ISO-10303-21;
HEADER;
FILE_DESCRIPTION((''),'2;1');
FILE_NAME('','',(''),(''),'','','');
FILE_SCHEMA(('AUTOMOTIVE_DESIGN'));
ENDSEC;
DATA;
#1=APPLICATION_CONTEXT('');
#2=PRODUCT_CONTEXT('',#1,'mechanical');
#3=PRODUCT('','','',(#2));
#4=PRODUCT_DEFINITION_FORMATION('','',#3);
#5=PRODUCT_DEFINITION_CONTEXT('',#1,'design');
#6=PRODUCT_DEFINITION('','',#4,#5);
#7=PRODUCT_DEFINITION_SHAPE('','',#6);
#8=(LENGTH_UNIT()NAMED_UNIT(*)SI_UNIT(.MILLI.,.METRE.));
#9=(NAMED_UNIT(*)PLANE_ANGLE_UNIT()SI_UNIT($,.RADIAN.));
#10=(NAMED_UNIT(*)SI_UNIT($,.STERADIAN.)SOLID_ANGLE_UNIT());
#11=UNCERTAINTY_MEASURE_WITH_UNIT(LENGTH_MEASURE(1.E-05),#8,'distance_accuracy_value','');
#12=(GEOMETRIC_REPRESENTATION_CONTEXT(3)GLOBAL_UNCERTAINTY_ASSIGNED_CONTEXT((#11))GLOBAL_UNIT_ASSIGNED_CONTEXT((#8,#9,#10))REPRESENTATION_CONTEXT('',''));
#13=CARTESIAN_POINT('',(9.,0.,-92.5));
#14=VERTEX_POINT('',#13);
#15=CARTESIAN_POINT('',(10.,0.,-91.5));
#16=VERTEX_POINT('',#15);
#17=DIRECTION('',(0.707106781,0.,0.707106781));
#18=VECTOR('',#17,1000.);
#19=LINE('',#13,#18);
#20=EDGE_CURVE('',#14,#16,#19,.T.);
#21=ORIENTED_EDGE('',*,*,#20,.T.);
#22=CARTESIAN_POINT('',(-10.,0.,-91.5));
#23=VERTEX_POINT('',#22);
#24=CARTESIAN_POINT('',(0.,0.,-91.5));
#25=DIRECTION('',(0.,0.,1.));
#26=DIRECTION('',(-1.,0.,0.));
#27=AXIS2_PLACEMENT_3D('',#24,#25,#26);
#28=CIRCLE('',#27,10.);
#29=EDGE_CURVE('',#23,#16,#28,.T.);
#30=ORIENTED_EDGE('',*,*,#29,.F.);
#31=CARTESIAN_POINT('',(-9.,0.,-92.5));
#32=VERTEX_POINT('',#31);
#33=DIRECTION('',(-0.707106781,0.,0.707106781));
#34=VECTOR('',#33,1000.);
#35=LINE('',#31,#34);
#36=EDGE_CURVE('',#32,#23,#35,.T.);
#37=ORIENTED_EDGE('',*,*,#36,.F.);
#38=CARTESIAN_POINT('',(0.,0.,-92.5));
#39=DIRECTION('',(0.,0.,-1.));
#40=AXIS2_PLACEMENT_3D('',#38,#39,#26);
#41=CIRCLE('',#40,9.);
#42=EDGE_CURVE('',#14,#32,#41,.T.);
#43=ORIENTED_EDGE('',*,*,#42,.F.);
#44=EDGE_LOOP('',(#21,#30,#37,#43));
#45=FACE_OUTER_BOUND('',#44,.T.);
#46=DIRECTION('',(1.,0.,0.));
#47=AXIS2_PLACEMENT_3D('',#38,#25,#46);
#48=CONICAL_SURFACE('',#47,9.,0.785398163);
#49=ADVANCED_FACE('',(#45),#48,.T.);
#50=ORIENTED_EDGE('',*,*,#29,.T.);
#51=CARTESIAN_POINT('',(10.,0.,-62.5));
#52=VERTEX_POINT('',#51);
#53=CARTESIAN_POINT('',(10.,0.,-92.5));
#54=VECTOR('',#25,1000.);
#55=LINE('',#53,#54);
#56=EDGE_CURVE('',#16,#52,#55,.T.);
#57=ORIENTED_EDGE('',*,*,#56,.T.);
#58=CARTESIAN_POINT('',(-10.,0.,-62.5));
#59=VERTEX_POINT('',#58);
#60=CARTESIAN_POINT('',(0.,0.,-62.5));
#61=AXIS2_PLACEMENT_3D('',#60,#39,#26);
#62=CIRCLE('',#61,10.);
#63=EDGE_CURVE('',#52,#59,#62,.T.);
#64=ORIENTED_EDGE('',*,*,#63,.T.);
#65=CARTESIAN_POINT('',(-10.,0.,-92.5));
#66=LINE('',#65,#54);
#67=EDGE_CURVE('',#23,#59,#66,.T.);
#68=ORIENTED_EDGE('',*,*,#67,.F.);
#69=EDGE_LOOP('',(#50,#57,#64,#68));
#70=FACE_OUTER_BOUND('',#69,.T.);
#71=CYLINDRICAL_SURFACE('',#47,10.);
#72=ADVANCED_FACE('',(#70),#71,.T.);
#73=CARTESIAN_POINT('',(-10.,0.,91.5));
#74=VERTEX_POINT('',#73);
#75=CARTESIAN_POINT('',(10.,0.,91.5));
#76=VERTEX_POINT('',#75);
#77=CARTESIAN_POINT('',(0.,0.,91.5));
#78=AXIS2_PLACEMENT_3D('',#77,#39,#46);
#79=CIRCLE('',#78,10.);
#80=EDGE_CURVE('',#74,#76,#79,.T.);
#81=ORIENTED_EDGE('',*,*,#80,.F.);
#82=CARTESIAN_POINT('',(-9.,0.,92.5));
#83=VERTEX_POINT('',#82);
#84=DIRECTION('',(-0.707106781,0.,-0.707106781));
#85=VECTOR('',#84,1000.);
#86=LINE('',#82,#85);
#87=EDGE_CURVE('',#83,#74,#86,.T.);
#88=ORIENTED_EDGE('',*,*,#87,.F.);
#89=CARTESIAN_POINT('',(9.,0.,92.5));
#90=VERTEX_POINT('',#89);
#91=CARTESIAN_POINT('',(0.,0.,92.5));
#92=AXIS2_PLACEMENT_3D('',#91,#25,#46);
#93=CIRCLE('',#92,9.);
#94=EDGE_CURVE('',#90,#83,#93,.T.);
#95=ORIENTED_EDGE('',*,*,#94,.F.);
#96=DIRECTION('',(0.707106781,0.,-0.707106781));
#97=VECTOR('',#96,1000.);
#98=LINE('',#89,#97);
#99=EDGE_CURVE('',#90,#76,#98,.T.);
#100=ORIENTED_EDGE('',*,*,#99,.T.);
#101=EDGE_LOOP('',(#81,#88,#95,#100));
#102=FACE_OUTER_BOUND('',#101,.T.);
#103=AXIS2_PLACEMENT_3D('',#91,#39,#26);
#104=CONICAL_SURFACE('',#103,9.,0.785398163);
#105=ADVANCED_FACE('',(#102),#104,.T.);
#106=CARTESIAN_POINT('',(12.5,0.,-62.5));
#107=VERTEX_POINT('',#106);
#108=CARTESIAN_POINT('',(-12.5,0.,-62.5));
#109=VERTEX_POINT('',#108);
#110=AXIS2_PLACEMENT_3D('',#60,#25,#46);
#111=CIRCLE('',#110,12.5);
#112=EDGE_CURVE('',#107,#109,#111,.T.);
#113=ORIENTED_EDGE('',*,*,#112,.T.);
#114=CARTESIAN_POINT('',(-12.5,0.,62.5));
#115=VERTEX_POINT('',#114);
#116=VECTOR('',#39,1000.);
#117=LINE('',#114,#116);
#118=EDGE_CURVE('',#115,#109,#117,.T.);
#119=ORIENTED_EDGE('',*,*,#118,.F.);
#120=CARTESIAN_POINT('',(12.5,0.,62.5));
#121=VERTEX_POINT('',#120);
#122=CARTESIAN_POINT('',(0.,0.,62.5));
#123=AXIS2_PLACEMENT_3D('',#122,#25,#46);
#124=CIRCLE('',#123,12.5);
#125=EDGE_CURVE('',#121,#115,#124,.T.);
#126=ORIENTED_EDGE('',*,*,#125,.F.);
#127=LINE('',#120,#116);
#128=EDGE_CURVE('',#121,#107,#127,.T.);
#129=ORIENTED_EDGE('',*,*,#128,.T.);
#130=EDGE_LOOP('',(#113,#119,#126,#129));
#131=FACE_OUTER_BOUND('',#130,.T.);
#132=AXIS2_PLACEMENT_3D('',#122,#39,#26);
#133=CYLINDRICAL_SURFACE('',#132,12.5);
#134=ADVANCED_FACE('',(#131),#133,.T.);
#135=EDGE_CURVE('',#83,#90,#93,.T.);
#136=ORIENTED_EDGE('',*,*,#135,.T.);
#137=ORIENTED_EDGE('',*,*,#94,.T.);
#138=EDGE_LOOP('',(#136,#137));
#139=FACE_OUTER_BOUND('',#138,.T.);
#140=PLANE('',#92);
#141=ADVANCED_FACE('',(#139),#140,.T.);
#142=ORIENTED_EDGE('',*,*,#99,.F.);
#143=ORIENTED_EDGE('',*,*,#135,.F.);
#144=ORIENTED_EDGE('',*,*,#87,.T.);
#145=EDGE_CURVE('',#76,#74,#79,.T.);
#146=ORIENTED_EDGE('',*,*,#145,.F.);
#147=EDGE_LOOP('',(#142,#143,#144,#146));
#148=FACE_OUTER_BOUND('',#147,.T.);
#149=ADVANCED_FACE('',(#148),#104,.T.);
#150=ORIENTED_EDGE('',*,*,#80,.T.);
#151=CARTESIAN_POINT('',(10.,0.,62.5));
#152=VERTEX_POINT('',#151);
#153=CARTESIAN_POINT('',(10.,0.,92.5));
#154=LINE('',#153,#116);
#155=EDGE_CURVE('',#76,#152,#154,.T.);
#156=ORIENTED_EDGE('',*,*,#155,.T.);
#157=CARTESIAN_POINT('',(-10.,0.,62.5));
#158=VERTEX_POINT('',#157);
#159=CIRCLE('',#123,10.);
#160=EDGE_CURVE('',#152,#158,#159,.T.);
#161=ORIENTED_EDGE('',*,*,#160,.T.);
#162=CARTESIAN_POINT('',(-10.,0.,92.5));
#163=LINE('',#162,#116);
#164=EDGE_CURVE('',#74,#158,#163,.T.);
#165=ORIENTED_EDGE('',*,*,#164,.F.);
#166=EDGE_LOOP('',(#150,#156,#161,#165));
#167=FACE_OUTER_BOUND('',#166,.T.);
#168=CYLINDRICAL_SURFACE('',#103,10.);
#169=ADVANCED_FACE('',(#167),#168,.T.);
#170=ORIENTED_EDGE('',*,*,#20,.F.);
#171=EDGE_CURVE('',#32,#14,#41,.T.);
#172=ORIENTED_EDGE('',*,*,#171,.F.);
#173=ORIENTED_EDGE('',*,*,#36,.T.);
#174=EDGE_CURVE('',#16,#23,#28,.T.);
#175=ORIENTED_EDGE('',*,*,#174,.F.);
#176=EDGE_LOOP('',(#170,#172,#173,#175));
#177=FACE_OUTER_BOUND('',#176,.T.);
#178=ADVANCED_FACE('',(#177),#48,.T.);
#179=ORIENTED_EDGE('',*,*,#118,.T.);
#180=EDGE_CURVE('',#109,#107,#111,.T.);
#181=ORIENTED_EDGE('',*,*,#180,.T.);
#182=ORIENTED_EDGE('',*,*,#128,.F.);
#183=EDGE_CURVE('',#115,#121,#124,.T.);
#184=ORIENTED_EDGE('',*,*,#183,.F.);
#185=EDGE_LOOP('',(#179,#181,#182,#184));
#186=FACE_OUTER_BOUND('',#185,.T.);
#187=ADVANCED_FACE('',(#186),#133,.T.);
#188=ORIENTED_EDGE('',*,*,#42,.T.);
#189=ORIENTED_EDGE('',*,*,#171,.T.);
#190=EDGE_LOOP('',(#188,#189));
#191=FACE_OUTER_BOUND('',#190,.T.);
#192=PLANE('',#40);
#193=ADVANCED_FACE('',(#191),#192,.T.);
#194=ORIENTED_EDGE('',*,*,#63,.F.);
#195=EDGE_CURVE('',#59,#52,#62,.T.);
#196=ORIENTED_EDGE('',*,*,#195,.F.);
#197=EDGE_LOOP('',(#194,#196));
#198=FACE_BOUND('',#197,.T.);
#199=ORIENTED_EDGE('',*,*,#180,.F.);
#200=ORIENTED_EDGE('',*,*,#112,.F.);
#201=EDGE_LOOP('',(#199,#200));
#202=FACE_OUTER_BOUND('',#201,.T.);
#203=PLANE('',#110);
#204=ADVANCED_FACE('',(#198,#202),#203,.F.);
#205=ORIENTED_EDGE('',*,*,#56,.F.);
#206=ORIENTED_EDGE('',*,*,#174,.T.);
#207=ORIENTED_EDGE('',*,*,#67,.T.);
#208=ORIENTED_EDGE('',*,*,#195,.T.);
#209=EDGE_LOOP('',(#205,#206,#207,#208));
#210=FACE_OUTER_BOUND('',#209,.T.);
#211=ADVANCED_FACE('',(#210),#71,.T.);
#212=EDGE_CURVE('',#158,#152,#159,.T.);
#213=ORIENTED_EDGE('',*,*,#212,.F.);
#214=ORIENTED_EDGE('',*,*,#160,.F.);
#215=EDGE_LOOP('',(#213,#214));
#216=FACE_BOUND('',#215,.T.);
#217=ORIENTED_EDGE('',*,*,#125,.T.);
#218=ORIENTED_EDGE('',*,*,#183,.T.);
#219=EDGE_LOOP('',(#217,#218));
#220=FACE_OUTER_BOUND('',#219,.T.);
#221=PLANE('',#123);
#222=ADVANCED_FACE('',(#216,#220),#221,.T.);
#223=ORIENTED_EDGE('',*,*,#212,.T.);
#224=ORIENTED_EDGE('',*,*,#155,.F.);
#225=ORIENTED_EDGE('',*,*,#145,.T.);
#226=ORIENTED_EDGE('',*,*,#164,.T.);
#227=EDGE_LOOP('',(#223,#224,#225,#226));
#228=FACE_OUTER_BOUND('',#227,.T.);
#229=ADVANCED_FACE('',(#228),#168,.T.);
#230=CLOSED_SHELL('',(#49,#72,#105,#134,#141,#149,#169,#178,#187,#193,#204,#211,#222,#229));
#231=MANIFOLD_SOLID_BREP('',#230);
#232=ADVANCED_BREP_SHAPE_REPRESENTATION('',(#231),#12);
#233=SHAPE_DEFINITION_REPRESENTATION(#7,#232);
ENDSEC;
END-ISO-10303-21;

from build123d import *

# Parameters (mm, degrees)
SKETCH1_R           = 12.5
BOSS_EXTRUDE1_DEPTH = 62.5
SKETCH2_R           = 10
BOSS_EXTRUDE2_DEPTH = 30
BOSS_EXTRUDE3_START = 30
SKETCH3_R           = 10
BOSS_EXTRUDE3_DEPTH = 30
CHAMFER1_SIZE       = 1


with BuildPart() as part:
    # Sketch1 → Boss-Extrude1 (new, symmetric)
    with BuildSketch(Plane.XY):
        Circle(SKETCH1_R)
    extrude(amount=BOSS_EXTRUDE1_DEPTH, both=True)

    # Sketch2 → Boss-Extrude2 (add)
    with BuildSketch(Plane.XY.offset(62.5)):
        Circle(SKETCH2_R)
    extrude(amount=BOSS_EXTRUDE2_DEPTH)

    # Sketch3 → Boss-Extrude3 (add)
    with BuildSketch(Plane(origin=(0, 0, -62.5), x_dir=(-1, 0, 0), z_dir=(0, 0, -1)).offset(BOSS_EXTRUDE3_START)):
        with Locations(Location((0, 0, 0), (0, 0, 180))):
            Circle(SKETCH3_R)
    extrude(amount=-BOSS_EXTRUDE3_DEPTH)

    # Chamfer1
    chamfer1_edges = [part.edges().sort_by_distance(p)[0] for p in [
        (-10, 0, -92.5),
        (-10, 0, 92.5),
    ]]
    chamfer(chamfer1_edges, length=CHAMFER1_SIZE)


solid = part.part
